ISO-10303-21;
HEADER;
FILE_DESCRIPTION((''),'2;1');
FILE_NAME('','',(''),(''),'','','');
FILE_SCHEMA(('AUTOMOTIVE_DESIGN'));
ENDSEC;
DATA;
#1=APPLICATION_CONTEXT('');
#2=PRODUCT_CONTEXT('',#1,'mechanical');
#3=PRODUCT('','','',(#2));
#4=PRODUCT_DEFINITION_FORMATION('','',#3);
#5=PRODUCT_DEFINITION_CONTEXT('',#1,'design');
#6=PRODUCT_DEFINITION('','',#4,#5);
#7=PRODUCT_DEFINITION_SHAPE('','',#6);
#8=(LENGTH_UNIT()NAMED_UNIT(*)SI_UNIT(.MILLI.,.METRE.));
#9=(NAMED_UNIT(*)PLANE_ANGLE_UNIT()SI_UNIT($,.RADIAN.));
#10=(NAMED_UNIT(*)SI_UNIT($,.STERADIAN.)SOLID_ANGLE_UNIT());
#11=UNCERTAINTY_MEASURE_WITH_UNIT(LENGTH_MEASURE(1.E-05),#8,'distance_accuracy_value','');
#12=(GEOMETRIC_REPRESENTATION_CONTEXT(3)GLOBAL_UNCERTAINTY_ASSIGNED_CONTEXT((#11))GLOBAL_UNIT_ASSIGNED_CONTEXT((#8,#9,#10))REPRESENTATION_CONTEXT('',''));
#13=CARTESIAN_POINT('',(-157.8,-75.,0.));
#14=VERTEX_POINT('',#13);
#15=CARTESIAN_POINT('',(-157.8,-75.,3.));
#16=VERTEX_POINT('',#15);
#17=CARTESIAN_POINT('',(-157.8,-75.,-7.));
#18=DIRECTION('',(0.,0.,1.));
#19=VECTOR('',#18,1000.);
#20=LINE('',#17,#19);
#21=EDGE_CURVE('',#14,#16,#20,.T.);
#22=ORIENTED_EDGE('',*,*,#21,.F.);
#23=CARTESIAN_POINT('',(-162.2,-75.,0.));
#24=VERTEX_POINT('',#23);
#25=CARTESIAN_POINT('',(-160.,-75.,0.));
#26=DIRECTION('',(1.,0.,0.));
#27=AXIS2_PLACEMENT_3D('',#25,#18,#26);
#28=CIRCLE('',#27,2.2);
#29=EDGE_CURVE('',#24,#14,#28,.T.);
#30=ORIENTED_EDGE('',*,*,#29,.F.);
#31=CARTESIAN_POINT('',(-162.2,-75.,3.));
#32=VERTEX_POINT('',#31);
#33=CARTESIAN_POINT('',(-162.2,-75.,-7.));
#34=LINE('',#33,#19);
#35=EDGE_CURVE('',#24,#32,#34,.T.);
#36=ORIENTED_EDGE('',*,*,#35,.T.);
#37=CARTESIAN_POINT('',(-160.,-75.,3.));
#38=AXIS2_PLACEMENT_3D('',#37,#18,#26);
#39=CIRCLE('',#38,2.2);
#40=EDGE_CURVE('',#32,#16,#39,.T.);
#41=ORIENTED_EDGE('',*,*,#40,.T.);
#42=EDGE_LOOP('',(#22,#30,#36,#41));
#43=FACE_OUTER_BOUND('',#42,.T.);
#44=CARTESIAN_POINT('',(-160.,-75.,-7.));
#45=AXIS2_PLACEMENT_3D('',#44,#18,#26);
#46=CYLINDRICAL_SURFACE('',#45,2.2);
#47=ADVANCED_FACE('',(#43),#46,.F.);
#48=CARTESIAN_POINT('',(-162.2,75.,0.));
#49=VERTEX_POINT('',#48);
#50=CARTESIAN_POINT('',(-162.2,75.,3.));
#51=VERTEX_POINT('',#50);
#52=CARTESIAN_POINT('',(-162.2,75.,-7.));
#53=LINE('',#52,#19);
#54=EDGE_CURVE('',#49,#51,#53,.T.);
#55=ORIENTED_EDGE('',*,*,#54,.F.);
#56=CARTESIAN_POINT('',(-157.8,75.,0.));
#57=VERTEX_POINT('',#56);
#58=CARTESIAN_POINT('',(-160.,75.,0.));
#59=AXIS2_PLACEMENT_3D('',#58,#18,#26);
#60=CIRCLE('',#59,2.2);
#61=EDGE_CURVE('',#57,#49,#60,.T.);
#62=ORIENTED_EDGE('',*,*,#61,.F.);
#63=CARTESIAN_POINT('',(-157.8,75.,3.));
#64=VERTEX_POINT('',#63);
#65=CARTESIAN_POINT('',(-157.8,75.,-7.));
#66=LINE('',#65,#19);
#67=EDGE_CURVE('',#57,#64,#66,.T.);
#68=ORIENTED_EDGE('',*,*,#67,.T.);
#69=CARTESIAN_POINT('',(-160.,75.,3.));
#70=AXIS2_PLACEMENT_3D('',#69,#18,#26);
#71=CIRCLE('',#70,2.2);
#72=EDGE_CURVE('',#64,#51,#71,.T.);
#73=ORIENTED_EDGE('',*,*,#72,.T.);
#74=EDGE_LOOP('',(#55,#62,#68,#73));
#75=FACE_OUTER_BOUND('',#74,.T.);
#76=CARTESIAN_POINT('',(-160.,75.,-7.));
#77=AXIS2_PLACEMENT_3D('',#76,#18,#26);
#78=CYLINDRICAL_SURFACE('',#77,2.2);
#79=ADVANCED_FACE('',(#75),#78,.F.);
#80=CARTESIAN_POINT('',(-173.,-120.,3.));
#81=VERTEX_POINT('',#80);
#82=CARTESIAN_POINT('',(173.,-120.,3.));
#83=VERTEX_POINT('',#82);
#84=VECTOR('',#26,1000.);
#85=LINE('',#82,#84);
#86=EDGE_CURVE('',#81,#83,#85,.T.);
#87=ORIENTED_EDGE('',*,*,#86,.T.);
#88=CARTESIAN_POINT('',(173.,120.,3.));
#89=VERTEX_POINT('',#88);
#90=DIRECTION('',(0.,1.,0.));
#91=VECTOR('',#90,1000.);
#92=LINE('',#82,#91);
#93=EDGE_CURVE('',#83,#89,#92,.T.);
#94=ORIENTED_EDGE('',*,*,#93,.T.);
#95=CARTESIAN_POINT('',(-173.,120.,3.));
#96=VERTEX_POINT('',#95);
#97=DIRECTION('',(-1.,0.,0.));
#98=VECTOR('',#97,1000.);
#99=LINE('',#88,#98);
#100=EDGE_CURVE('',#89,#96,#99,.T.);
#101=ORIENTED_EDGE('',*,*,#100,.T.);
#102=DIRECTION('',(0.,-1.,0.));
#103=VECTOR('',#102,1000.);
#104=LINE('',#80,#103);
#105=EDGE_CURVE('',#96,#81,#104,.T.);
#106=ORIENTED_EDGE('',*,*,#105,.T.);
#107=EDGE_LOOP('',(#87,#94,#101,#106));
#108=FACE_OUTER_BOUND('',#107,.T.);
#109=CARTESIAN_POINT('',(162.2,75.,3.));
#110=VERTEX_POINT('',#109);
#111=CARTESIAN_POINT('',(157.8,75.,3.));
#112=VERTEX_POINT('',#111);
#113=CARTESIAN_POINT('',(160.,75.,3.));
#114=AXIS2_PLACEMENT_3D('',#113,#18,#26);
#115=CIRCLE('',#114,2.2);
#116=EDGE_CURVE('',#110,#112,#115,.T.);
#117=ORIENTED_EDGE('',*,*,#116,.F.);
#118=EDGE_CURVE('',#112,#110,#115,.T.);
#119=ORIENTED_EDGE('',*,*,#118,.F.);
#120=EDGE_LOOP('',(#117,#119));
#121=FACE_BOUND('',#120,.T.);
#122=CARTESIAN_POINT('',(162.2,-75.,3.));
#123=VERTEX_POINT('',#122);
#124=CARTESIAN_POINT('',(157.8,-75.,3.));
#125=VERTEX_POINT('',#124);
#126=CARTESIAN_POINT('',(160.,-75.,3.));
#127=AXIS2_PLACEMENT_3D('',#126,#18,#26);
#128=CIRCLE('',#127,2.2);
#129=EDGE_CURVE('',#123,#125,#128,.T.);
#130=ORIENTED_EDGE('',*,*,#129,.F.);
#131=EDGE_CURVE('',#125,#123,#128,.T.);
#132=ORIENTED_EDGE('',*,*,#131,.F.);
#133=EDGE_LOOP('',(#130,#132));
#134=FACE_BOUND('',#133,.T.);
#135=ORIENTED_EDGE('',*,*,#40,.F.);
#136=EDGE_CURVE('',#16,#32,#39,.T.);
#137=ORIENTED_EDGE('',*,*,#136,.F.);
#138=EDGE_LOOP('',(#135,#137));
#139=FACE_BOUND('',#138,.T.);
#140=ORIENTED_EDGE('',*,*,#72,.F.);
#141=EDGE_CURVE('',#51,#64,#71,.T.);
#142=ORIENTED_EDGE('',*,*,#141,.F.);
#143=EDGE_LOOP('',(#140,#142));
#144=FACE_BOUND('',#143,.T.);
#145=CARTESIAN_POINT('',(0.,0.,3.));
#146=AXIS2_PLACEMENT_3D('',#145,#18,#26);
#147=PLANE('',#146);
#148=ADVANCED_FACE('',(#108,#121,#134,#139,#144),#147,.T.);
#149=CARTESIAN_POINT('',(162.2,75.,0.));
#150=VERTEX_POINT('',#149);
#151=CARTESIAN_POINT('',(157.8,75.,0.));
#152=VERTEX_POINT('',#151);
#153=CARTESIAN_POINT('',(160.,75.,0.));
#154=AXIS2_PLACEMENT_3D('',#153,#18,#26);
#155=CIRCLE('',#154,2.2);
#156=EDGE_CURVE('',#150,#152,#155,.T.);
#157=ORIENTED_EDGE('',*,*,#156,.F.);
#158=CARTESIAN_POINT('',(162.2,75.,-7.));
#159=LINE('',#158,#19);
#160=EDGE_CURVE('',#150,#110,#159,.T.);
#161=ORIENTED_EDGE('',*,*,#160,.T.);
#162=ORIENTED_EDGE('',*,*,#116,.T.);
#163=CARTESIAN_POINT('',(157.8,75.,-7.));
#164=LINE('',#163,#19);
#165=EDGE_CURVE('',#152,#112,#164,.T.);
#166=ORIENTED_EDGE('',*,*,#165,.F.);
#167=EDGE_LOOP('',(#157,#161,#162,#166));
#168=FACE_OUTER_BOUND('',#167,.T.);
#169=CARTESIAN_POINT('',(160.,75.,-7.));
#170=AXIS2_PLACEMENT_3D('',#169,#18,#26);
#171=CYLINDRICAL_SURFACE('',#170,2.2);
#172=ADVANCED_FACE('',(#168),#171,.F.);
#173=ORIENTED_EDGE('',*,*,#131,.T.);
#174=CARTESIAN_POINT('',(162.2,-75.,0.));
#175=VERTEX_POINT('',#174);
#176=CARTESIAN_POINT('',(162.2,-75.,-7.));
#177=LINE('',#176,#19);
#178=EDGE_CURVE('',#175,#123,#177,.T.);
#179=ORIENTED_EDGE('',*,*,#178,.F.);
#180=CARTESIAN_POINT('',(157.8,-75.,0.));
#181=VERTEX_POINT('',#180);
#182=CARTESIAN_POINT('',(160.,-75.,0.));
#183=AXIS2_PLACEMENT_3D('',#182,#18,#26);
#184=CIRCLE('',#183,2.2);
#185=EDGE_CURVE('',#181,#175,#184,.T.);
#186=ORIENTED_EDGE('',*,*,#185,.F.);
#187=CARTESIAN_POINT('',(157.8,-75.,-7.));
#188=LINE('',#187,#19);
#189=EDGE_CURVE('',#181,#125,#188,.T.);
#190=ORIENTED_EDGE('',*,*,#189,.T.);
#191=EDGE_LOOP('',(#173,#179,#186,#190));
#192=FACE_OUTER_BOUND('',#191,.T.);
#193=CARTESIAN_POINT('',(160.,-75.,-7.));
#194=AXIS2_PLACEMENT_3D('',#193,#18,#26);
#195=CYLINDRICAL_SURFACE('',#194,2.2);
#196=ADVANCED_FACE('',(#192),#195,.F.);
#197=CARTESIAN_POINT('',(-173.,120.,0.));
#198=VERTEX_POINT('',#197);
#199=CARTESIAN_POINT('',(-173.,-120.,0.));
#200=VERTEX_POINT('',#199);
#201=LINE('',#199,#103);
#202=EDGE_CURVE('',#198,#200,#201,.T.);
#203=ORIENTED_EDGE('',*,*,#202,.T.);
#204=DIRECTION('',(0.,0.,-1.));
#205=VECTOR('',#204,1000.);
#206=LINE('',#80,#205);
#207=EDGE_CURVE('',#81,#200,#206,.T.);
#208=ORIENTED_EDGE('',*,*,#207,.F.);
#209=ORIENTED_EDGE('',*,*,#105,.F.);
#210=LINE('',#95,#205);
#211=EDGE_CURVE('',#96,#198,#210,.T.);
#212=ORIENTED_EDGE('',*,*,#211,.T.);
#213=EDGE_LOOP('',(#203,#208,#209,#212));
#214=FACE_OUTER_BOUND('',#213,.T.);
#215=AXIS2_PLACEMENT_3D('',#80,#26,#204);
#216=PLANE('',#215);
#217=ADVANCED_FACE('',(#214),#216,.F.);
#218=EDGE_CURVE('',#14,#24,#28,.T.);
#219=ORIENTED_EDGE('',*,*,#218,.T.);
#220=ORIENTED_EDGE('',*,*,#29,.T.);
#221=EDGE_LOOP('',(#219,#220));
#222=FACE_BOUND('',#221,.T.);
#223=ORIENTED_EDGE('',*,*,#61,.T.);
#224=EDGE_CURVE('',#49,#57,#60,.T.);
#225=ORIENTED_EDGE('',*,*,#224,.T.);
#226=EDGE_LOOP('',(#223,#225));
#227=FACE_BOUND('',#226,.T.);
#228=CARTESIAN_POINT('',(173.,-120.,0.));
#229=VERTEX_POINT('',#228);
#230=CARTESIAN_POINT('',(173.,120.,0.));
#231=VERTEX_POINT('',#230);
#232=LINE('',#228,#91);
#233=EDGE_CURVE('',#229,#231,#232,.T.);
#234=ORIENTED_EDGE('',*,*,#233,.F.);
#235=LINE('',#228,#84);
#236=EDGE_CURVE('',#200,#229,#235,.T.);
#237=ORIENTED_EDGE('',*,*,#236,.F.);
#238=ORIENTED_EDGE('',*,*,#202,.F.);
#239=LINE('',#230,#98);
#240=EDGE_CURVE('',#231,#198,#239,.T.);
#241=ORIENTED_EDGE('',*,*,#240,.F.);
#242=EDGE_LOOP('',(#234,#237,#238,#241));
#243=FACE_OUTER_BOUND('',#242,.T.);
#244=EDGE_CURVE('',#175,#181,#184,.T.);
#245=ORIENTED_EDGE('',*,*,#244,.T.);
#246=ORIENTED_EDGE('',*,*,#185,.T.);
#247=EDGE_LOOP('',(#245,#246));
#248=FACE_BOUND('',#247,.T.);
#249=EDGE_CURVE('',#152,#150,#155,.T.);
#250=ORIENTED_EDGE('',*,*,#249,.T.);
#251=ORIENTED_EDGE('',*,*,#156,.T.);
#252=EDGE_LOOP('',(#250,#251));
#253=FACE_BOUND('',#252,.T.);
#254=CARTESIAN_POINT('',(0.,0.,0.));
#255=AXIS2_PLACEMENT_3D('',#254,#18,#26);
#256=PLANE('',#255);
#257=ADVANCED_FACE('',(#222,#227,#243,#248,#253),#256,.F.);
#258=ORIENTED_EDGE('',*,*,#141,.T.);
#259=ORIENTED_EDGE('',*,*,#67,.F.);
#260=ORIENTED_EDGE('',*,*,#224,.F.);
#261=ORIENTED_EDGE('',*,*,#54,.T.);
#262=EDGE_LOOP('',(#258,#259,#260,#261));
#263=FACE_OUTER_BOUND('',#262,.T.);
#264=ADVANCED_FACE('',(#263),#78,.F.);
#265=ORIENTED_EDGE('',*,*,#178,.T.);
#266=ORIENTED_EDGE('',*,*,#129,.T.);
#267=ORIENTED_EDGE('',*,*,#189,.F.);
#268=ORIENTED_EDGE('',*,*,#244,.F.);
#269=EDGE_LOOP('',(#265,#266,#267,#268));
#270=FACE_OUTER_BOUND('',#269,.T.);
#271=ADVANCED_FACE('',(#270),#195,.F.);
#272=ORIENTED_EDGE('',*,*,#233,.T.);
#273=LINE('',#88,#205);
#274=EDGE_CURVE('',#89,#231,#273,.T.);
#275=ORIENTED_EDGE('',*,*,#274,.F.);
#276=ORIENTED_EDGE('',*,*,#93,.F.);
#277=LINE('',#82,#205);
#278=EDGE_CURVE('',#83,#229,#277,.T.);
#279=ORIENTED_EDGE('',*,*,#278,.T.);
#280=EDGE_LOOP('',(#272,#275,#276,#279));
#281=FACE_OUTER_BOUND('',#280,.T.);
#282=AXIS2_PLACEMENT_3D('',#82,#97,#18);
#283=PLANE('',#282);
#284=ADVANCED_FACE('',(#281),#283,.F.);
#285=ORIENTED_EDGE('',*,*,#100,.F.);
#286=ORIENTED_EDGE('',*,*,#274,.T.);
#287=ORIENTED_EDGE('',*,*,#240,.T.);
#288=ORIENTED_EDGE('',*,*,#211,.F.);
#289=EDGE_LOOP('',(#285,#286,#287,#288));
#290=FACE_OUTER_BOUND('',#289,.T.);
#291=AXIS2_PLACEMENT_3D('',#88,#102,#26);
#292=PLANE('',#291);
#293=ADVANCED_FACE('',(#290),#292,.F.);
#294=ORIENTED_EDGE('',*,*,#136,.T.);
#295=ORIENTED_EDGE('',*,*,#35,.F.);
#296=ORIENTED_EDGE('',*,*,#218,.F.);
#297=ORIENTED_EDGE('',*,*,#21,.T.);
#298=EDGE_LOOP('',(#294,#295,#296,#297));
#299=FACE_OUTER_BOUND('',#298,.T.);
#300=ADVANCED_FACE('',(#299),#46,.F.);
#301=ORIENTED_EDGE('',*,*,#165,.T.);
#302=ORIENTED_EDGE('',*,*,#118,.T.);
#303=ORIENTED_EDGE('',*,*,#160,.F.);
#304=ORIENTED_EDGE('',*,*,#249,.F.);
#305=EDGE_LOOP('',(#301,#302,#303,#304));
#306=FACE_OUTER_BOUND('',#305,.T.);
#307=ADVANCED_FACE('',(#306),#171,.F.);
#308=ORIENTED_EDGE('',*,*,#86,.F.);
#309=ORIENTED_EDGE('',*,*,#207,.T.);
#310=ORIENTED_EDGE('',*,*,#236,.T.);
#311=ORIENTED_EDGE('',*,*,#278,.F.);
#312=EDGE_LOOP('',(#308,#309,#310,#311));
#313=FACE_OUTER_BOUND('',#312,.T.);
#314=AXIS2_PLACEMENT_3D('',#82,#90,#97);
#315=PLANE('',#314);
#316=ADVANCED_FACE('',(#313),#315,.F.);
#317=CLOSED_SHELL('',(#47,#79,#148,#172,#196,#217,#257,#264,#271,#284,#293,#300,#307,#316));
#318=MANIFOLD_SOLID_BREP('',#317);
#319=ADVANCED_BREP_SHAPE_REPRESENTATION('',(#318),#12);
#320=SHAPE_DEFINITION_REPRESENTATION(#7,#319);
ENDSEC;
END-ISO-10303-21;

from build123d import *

# Parameters (mm, degrees)
SKETCH_1_W          = 346
SKETCH_1_H          = 240
EXTRUDE_1_DEPTH     = 3
SKETCH_2_R          = 2.2
CUT_EXTRUDE_1_DEPTH = 10


with BuildPart() as part:
    # 草图1 → 凸台-拉伸1 (new body)
    with BuildSketch(Plane.XY):
        Rectangle(SKETCH_1_W, SKETCH_1_H)
    extrude(amount=EXTRUDE_1_DEPTH)

    # 草图2 → 切除-拉伸1 (cut)
    with BuildSketch(Plane.XY.offset(3)):
        with Locations((160, 75)):
            Circle(SKETCH_2_R)
        with Locations((160, -75)):
            Circle(SKETCH_2_R)
        with Locations((-160, 75)):
            Circle(SKETCH_2_R)
        with Locations((-160, -75)):
            Circle(SKETCH_2_R)
        with Locations((-199.409999505, 140.432462879)):
            Circle(SKETCH_2_R)
        with Locations((-199.409999505, -9.567537121)):
            Circle(SKETCH_2_R)
    extrude(amount=-CUT_EXTRUDE_1_DEPTH, mode=Mode.SUBTRACT)


solid = part.part
